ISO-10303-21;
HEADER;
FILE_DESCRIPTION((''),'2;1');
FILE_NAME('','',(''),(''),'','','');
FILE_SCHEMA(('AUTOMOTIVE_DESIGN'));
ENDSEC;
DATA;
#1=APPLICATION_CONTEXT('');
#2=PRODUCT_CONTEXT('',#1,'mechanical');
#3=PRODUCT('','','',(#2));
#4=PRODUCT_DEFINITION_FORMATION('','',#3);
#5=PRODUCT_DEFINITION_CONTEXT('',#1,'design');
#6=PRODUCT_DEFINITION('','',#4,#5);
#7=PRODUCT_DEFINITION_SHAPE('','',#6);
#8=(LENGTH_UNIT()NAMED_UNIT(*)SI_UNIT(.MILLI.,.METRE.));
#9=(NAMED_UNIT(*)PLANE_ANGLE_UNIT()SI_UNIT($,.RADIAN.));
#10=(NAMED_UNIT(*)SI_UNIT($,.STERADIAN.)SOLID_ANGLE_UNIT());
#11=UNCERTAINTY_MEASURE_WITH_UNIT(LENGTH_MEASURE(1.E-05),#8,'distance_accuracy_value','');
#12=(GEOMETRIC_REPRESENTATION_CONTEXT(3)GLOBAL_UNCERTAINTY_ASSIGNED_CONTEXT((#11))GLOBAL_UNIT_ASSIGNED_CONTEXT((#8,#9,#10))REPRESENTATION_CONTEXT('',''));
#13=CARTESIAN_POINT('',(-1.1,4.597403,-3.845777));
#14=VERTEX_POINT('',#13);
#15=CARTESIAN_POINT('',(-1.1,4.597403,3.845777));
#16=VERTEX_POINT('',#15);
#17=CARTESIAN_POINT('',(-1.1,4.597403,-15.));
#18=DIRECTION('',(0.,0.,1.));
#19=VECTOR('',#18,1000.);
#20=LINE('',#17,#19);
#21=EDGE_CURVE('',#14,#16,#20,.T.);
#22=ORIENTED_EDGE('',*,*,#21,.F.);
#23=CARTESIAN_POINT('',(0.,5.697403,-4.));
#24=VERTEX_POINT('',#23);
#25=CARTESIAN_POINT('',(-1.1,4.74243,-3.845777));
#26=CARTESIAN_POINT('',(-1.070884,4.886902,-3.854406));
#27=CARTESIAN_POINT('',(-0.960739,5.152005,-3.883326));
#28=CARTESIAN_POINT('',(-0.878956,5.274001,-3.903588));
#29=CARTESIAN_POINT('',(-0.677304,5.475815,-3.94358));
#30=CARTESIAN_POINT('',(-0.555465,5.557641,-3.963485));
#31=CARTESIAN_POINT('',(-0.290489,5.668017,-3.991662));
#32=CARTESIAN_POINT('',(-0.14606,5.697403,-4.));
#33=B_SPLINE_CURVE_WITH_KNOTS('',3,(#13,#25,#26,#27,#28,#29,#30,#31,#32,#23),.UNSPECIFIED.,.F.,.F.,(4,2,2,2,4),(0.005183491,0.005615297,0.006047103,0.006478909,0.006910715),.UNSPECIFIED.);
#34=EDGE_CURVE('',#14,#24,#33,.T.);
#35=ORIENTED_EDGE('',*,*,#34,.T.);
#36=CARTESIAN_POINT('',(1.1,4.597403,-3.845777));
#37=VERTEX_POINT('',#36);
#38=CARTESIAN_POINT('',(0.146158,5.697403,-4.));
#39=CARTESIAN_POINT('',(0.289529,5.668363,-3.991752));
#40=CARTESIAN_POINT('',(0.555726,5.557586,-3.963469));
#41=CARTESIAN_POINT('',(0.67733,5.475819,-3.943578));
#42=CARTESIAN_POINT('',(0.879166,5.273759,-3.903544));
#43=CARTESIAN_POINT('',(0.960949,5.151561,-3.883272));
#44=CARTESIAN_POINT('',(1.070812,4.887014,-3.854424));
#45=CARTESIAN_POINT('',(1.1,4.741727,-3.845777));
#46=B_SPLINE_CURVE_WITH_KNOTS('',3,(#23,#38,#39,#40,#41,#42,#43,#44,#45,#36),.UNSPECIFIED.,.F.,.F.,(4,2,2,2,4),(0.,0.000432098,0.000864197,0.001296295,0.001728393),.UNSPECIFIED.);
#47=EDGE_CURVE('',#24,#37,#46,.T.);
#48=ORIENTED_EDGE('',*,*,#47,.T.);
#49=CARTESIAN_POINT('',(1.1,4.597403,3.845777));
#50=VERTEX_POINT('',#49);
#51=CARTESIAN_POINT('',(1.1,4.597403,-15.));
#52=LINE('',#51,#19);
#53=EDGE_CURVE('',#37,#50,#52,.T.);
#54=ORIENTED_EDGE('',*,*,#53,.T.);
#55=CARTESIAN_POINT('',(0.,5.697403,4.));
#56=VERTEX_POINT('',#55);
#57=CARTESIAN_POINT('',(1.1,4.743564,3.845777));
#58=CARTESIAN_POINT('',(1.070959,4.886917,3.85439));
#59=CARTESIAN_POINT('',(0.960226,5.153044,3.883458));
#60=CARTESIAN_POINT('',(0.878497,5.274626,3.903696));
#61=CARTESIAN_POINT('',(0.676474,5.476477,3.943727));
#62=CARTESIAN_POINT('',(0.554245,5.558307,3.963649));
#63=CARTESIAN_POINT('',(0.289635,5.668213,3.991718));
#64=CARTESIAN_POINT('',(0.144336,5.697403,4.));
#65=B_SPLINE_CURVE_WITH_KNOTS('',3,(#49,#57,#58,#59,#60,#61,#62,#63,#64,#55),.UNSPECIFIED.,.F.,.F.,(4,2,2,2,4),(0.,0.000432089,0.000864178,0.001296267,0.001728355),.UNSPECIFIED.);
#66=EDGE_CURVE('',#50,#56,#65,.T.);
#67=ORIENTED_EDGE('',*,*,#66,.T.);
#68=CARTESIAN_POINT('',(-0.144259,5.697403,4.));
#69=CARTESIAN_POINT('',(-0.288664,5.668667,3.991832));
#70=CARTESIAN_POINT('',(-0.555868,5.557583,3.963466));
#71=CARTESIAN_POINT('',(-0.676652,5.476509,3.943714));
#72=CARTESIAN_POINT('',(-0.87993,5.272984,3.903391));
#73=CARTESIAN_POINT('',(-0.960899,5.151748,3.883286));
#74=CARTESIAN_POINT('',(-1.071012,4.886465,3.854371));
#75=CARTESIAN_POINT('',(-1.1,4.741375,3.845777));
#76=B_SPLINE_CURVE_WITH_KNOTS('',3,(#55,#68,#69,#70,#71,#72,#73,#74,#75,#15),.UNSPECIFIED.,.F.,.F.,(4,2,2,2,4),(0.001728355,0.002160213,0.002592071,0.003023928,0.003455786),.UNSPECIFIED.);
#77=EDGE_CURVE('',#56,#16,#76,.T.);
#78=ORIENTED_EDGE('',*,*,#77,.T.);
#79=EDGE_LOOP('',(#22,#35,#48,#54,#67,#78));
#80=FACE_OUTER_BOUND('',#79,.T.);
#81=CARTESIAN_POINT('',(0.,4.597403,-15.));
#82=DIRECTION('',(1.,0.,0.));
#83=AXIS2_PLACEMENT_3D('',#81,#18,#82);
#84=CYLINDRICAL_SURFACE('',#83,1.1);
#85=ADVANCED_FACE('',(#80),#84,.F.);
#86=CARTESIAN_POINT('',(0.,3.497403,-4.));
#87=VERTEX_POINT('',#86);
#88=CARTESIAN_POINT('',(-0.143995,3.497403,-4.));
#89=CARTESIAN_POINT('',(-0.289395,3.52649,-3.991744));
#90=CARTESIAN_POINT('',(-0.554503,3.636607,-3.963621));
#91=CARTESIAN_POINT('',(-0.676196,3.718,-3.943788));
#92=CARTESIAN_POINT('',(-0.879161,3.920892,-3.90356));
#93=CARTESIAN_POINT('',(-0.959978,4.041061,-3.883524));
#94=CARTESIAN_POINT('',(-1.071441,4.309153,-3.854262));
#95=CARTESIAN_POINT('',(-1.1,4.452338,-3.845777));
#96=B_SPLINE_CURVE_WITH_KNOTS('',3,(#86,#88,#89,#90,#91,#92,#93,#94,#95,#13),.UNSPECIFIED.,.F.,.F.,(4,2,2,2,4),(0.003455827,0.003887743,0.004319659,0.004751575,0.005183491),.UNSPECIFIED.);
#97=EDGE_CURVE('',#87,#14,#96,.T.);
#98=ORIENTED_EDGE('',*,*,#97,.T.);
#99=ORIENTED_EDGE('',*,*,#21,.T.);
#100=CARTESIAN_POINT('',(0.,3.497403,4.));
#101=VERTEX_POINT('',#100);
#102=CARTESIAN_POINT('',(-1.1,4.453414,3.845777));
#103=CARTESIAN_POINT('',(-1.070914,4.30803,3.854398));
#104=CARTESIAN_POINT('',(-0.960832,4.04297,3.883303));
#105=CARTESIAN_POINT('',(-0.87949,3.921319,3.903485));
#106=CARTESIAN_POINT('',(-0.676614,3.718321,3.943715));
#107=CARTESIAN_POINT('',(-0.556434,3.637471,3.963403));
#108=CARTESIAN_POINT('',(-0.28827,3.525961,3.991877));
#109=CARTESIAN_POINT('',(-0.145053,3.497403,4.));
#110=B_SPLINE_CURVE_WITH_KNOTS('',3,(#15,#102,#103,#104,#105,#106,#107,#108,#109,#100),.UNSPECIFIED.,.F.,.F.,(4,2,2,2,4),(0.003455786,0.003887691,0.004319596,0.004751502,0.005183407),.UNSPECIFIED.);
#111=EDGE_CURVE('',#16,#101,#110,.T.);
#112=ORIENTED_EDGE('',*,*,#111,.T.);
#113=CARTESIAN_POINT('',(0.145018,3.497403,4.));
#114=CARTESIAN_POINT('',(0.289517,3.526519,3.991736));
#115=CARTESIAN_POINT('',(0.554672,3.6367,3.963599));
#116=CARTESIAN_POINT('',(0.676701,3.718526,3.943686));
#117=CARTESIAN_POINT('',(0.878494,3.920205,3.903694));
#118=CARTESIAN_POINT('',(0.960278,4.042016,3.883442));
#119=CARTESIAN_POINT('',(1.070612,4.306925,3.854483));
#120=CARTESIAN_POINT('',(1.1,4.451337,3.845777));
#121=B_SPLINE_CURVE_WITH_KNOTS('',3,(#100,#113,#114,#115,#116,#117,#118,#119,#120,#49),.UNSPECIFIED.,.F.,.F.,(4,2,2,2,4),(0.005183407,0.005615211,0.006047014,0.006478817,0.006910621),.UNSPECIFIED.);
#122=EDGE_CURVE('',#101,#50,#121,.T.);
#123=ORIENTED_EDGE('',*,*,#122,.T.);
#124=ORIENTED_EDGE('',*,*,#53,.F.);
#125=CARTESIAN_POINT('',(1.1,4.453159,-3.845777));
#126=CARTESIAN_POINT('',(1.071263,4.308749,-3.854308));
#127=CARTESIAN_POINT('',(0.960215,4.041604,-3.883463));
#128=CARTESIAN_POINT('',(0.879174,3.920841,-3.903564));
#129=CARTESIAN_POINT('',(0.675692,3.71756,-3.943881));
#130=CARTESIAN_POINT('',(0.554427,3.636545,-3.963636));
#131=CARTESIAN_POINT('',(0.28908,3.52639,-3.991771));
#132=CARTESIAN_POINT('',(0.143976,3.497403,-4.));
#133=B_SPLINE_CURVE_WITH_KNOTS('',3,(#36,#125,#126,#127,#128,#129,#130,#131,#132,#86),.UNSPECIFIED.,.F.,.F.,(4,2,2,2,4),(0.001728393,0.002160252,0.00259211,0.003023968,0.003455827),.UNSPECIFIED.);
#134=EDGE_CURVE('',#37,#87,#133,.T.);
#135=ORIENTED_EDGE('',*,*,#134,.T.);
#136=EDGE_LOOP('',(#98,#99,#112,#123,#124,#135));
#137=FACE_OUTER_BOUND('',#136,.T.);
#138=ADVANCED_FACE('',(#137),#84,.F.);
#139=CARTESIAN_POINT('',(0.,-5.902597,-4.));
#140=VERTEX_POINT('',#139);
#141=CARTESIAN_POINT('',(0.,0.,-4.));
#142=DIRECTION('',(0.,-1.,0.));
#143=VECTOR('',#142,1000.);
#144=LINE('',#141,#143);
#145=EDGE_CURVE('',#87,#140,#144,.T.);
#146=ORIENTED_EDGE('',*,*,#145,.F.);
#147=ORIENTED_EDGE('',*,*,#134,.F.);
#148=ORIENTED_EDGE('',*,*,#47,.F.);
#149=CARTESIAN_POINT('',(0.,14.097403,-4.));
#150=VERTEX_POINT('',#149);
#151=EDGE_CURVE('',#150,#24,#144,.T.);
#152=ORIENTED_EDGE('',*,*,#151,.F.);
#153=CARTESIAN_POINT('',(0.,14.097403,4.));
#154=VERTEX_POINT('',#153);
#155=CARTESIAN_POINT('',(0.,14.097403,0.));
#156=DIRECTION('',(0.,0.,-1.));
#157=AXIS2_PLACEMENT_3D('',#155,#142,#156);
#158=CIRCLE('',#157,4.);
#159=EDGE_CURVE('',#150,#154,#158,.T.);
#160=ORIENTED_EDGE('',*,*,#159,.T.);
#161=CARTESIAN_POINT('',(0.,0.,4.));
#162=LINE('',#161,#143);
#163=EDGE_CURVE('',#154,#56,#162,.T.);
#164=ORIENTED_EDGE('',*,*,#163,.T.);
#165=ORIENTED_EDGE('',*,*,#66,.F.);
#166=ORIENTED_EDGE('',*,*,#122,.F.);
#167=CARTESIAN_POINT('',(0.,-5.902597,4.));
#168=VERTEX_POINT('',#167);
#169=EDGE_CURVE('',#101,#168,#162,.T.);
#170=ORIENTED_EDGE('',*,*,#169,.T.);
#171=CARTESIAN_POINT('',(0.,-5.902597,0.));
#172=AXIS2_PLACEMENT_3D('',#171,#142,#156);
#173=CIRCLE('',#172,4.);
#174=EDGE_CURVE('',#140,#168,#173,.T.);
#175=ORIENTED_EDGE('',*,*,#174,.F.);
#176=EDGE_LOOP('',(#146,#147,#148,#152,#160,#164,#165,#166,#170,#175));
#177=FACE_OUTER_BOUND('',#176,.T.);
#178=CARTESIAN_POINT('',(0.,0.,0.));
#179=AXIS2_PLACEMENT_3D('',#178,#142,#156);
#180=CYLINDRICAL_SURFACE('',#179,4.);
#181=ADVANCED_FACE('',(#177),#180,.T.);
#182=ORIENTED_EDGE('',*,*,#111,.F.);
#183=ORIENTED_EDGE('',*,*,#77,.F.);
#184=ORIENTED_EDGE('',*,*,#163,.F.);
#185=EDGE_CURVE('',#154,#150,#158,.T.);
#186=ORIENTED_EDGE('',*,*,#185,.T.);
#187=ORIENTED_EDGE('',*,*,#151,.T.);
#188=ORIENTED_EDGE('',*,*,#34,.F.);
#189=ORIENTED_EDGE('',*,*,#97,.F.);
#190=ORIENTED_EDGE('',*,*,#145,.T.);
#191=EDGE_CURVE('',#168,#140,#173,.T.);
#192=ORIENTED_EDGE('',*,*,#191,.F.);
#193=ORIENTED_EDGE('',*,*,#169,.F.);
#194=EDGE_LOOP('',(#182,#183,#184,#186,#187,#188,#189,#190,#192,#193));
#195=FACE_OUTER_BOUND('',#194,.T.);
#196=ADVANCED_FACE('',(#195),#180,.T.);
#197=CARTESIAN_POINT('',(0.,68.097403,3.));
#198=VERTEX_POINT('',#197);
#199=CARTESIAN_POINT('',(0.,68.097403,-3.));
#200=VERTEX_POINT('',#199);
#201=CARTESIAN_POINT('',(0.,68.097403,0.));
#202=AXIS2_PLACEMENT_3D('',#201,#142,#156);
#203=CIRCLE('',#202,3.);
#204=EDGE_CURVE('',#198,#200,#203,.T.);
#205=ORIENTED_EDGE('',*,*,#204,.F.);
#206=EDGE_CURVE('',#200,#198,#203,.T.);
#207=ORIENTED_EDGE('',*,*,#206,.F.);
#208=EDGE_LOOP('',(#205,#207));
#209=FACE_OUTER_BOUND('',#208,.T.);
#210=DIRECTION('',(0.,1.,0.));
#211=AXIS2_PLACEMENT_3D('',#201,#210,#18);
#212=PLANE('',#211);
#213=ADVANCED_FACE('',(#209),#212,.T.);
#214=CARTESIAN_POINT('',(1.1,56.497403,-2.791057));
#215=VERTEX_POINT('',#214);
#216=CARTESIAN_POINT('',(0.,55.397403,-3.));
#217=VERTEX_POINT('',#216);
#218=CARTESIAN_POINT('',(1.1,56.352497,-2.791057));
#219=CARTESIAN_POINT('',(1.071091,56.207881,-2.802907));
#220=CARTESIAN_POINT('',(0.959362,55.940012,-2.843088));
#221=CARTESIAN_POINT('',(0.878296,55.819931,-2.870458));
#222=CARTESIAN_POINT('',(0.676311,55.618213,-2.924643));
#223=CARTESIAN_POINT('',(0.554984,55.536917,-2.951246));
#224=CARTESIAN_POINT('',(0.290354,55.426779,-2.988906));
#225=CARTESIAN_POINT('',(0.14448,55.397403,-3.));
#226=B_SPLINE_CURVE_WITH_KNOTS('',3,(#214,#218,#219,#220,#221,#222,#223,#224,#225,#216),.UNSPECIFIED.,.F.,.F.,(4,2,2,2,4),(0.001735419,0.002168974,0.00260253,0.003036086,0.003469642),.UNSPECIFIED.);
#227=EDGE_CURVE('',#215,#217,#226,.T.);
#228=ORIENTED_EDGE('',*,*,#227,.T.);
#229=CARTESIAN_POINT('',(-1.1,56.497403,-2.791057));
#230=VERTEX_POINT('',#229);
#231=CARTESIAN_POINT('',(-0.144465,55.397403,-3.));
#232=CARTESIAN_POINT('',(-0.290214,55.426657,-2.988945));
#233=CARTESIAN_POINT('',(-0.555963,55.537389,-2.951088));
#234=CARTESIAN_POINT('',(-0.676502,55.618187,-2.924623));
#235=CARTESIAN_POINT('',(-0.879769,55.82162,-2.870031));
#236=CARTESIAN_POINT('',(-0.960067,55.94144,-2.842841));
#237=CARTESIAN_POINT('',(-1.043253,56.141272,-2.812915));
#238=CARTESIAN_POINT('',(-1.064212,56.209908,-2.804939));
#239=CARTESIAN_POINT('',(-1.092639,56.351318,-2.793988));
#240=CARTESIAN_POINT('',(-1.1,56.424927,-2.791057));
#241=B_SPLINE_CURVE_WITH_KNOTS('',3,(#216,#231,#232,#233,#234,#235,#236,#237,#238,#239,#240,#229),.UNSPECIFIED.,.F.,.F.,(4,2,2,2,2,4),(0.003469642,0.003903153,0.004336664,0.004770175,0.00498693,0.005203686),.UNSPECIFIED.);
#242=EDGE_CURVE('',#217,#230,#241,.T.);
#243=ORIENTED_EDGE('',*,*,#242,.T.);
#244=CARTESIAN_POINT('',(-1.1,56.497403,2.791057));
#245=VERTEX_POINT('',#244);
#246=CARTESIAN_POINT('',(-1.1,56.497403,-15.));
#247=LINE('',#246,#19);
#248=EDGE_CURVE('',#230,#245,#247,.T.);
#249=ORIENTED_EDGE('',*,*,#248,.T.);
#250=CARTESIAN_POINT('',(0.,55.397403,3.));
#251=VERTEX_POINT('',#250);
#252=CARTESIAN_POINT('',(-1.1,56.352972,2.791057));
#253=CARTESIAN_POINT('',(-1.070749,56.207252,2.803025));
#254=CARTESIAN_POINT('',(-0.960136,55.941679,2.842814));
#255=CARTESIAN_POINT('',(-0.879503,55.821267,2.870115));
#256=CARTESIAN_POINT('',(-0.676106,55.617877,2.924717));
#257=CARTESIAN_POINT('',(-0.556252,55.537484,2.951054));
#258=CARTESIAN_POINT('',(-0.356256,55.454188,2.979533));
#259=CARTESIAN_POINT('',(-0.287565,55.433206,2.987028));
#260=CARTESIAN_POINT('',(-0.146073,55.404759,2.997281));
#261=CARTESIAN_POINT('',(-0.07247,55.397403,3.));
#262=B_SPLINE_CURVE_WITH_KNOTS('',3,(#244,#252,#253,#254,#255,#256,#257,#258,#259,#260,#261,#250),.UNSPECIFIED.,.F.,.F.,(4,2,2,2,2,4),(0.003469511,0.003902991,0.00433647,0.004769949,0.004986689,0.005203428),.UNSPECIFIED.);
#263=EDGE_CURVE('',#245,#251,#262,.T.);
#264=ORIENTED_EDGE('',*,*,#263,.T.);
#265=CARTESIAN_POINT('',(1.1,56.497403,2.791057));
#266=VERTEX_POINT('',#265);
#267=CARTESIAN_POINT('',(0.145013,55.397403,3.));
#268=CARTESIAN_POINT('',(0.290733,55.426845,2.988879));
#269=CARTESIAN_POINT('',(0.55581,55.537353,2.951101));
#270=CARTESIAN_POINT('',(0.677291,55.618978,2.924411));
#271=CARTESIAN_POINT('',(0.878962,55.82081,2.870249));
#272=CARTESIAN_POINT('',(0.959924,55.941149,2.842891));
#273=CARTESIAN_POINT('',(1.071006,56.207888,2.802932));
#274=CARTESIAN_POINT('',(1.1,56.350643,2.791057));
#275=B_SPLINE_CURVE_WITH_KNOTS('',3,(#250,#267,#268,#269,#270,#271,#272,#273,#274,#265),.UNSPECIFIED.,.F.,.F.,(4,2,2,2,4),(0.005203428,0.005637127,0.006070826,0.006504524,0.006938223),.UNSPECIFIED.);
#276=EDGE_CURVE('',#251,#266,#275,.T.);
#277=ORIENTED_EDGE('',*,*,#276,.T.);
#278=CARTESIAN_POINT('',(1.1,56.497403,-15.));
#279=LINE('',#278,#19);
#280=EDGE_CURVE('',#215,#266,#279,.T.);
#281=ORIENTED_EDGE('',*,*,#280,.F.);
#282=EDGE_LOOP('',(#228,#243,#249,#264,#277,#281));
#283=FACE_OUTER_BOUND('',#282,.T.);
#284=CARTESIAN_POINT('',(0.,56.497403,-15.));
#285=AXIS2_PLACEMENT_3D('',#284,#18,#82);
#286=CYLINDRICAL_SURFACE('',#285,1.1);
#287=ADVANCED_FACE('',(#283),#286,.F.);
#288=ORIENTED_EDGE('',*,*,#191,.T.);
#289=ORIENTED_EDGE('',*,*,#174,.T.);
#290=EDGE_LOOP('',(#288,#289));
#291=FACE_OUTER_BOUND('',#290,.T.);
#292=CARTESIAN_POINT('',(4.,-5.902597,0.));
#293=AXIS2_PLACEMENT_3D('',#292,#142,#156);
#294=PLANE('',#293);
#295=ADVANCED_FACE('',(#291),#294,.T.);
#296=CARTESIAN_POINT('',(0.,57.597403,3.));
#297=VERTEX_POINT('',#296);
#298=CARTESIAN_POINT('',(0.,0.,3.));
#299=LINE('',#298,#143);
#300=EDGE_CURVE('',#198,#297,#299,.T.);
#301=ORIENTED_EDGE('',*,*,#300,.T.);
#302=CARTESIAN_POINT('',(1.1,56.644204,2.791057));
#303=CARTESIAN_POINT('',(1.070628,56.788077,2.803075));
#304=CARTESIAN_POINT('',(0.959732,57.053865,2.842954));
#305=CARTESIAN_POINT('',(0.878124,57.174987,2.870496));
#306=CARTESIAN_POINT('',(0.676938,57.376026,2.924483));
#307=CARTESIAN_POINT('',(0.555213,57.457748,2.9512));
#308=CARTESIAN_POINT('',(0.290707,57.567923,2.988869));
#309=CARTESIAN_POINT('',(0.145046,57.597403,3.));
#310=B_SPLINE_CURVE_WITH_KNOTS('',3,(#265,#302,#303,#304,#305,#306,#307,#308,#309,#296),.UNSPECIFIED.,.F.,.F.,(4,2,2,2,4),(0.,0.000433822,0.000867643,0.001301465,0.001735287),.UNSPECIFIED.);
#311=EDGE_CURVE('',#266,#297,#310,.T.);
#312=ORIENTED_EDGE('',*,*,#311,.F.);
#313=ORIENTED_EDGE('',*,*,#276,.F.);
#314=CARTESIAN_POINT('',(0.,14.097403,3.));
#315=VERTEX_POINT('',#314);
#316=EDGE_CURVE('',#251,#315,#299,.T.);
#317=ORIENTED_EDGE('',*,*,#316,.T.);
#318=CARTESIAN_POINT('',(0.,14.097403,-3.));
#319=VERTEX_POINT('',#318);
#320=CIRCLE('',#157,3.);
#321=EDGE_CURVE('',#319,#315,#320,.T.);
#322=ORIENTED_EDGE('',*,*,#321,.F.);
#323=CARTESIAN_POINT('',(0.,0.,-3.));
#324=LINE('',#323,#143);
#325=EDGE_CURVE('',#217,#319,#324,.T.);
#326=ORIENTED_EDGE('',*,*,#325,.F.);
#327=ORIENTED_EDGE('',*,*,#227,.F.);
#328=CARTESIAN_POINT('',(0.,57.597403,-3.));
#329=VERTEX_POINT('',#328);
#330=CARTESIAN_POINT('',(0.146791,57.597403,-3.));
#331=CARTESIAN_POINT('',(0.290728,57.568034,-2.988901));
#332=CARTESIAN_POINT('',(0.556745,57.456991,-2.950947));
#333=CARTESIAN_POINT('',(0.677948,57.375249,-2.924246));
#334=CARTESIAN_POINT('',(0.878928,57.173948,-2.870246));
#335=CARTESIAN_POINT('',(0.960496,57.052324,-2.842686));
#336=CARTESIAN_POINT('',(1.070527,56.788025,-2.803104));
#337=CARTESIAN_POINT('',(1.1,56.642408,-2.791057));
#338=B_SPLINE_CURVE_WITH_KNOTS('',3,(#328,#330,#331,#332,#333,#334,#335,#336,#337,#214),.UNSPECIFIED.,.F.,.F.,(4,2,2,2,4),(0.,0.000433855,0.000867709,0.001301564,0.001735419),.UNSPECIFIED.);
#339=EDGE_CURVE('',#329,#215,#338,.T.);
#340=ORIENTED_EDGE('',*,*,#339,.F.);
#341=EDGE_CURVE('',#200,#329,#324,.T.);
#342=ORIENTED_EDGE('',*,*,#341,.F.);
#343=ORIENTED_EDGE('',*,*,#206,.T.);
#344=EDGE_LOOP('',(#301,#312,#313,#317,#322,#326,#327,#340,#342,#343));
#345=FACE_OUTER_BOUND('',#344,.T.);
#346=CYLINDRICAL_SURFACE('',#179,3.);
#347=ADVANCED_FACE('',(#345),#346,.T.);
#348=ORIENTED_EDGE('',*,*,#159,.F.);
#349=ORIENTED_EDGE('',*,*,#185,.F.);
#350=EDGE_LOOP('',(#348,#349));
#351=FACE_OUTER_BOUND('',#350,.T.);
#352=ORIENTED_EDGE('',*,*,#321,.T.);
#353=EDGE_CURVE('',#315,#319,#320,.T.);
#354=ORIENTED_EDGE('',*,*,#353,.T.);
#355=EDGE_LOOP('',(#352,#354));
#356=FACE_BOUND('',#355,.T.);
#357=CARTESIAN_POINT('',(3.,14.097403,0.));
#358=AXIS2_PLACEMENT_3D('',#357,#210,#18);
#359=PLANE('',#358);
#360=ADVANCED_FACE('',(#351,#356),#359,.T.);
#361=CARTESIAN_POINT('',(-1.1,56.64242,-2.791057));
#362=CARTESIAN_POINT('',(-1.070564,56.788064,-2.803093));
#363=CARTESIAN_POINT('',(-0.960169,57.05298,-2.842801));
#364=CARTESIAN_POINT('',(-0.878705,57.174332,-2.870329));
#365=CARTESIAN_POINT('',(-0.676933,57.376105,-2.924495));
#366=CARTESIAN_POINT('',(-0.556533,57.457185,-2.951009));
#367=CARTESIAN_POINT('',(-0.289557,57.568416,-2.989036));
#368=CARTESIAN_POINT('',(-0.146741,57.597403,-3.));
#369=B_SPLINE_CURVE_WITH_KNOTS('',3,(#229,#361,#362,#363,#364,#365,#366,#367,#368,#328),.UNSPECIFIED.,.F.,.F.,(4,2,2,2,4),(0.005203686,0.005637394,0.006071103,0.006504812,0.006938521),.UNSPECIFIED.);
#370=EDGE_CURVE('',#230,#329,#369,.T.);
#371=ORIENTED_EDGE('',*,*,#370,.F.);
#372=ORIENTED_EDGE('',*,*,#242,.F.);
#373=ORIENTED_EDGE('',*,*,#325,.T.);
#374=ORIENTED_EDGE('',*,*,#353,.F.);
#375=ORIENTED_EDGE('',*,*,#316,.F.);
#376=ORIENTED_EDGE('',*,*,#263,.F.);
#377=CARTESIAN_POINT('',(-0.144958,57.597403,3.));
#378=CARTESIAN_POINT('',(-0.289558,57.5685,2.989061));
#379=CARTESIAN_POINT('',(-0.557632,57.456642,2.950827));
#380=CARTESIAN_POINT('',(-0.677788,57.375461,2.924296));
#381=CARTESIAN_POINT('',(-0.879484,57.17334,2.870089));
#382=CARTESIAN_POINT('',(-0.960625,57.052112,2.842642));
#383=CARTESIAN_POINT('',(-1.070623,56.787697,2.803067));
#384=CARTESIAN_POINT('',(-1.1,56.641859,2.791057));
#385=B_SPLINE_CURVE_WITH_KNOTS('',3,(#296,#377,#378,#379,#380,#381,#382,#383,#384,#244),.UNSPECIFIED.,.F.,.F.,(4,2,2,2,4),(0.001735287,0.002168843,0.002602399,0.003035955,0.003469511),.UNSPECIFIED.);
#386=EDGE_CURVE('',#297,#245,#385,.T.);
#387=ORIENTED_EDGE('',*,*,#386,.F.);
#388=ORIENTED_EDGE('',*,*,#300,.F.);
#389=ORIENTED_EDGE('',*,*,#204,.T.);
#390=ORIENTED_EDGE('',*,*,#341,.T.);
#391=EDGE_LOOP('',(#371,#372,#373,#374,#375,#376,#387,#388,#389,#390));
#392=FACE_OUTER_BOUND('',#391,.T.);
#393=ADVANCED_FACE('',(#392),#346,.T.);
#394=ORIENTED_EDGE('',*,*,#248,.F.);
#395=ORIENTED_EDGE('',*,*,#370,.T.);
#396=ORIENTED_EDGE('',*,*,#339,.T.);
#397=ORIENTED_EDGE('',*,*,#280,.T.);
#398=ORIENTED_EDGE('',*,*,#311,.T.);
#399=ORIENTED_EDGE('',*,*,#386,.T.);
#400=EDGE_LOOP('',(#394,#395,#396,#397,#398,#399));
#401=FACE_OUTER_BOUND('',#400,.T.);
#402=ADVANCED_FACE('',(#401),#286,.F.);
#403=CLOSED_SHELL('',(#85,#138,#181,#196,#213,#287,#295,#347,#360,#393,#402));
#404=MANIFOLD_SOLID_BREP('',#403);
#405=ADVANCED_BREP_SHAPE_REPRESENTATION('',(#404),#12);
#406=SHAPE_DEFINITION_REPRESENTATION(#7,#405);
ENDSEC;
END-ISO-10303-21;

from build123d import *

# Parameters (mm, degrees)
SKETCH_2_R          = 1.1
CUT_EXTRUDE_1_DEPTH = 15


with BuildPart() as part:
    # 草图1 → 旋转1 (revolve)
    with BuildSketch(Plane.XY, mode=Mode.PRIVATE) as revolve_1_sk:
        Polygon((0, 68.097402597), (3, 68.097402597), (3, 14.097402597), (4, 14.097402597), (4, -5.902597403), (0, -5.902597403), align=None)
    revolve(revolve_1_sk.sketch.rotate(Axis((0, 0, 0), (0, 1, 0)), 90), axis=Axis((0, 0, 0), (0, 1, 0)))

    # 草图2 → 切除-拉伸1 (cut, symmetric)
    with BuildSketch(Plane.XY):
        with Locations((0, 56.497402597)):
            Circle(SKETCH_2_R)
        with Locations((0, 4.597402597)):
            Circle(SKETCH_2_R)
    extrude(amount=CUT_EXTRUDE_1_DEPTH, both=True, mode=Mode.SUBTRACT)


solid = part.part
